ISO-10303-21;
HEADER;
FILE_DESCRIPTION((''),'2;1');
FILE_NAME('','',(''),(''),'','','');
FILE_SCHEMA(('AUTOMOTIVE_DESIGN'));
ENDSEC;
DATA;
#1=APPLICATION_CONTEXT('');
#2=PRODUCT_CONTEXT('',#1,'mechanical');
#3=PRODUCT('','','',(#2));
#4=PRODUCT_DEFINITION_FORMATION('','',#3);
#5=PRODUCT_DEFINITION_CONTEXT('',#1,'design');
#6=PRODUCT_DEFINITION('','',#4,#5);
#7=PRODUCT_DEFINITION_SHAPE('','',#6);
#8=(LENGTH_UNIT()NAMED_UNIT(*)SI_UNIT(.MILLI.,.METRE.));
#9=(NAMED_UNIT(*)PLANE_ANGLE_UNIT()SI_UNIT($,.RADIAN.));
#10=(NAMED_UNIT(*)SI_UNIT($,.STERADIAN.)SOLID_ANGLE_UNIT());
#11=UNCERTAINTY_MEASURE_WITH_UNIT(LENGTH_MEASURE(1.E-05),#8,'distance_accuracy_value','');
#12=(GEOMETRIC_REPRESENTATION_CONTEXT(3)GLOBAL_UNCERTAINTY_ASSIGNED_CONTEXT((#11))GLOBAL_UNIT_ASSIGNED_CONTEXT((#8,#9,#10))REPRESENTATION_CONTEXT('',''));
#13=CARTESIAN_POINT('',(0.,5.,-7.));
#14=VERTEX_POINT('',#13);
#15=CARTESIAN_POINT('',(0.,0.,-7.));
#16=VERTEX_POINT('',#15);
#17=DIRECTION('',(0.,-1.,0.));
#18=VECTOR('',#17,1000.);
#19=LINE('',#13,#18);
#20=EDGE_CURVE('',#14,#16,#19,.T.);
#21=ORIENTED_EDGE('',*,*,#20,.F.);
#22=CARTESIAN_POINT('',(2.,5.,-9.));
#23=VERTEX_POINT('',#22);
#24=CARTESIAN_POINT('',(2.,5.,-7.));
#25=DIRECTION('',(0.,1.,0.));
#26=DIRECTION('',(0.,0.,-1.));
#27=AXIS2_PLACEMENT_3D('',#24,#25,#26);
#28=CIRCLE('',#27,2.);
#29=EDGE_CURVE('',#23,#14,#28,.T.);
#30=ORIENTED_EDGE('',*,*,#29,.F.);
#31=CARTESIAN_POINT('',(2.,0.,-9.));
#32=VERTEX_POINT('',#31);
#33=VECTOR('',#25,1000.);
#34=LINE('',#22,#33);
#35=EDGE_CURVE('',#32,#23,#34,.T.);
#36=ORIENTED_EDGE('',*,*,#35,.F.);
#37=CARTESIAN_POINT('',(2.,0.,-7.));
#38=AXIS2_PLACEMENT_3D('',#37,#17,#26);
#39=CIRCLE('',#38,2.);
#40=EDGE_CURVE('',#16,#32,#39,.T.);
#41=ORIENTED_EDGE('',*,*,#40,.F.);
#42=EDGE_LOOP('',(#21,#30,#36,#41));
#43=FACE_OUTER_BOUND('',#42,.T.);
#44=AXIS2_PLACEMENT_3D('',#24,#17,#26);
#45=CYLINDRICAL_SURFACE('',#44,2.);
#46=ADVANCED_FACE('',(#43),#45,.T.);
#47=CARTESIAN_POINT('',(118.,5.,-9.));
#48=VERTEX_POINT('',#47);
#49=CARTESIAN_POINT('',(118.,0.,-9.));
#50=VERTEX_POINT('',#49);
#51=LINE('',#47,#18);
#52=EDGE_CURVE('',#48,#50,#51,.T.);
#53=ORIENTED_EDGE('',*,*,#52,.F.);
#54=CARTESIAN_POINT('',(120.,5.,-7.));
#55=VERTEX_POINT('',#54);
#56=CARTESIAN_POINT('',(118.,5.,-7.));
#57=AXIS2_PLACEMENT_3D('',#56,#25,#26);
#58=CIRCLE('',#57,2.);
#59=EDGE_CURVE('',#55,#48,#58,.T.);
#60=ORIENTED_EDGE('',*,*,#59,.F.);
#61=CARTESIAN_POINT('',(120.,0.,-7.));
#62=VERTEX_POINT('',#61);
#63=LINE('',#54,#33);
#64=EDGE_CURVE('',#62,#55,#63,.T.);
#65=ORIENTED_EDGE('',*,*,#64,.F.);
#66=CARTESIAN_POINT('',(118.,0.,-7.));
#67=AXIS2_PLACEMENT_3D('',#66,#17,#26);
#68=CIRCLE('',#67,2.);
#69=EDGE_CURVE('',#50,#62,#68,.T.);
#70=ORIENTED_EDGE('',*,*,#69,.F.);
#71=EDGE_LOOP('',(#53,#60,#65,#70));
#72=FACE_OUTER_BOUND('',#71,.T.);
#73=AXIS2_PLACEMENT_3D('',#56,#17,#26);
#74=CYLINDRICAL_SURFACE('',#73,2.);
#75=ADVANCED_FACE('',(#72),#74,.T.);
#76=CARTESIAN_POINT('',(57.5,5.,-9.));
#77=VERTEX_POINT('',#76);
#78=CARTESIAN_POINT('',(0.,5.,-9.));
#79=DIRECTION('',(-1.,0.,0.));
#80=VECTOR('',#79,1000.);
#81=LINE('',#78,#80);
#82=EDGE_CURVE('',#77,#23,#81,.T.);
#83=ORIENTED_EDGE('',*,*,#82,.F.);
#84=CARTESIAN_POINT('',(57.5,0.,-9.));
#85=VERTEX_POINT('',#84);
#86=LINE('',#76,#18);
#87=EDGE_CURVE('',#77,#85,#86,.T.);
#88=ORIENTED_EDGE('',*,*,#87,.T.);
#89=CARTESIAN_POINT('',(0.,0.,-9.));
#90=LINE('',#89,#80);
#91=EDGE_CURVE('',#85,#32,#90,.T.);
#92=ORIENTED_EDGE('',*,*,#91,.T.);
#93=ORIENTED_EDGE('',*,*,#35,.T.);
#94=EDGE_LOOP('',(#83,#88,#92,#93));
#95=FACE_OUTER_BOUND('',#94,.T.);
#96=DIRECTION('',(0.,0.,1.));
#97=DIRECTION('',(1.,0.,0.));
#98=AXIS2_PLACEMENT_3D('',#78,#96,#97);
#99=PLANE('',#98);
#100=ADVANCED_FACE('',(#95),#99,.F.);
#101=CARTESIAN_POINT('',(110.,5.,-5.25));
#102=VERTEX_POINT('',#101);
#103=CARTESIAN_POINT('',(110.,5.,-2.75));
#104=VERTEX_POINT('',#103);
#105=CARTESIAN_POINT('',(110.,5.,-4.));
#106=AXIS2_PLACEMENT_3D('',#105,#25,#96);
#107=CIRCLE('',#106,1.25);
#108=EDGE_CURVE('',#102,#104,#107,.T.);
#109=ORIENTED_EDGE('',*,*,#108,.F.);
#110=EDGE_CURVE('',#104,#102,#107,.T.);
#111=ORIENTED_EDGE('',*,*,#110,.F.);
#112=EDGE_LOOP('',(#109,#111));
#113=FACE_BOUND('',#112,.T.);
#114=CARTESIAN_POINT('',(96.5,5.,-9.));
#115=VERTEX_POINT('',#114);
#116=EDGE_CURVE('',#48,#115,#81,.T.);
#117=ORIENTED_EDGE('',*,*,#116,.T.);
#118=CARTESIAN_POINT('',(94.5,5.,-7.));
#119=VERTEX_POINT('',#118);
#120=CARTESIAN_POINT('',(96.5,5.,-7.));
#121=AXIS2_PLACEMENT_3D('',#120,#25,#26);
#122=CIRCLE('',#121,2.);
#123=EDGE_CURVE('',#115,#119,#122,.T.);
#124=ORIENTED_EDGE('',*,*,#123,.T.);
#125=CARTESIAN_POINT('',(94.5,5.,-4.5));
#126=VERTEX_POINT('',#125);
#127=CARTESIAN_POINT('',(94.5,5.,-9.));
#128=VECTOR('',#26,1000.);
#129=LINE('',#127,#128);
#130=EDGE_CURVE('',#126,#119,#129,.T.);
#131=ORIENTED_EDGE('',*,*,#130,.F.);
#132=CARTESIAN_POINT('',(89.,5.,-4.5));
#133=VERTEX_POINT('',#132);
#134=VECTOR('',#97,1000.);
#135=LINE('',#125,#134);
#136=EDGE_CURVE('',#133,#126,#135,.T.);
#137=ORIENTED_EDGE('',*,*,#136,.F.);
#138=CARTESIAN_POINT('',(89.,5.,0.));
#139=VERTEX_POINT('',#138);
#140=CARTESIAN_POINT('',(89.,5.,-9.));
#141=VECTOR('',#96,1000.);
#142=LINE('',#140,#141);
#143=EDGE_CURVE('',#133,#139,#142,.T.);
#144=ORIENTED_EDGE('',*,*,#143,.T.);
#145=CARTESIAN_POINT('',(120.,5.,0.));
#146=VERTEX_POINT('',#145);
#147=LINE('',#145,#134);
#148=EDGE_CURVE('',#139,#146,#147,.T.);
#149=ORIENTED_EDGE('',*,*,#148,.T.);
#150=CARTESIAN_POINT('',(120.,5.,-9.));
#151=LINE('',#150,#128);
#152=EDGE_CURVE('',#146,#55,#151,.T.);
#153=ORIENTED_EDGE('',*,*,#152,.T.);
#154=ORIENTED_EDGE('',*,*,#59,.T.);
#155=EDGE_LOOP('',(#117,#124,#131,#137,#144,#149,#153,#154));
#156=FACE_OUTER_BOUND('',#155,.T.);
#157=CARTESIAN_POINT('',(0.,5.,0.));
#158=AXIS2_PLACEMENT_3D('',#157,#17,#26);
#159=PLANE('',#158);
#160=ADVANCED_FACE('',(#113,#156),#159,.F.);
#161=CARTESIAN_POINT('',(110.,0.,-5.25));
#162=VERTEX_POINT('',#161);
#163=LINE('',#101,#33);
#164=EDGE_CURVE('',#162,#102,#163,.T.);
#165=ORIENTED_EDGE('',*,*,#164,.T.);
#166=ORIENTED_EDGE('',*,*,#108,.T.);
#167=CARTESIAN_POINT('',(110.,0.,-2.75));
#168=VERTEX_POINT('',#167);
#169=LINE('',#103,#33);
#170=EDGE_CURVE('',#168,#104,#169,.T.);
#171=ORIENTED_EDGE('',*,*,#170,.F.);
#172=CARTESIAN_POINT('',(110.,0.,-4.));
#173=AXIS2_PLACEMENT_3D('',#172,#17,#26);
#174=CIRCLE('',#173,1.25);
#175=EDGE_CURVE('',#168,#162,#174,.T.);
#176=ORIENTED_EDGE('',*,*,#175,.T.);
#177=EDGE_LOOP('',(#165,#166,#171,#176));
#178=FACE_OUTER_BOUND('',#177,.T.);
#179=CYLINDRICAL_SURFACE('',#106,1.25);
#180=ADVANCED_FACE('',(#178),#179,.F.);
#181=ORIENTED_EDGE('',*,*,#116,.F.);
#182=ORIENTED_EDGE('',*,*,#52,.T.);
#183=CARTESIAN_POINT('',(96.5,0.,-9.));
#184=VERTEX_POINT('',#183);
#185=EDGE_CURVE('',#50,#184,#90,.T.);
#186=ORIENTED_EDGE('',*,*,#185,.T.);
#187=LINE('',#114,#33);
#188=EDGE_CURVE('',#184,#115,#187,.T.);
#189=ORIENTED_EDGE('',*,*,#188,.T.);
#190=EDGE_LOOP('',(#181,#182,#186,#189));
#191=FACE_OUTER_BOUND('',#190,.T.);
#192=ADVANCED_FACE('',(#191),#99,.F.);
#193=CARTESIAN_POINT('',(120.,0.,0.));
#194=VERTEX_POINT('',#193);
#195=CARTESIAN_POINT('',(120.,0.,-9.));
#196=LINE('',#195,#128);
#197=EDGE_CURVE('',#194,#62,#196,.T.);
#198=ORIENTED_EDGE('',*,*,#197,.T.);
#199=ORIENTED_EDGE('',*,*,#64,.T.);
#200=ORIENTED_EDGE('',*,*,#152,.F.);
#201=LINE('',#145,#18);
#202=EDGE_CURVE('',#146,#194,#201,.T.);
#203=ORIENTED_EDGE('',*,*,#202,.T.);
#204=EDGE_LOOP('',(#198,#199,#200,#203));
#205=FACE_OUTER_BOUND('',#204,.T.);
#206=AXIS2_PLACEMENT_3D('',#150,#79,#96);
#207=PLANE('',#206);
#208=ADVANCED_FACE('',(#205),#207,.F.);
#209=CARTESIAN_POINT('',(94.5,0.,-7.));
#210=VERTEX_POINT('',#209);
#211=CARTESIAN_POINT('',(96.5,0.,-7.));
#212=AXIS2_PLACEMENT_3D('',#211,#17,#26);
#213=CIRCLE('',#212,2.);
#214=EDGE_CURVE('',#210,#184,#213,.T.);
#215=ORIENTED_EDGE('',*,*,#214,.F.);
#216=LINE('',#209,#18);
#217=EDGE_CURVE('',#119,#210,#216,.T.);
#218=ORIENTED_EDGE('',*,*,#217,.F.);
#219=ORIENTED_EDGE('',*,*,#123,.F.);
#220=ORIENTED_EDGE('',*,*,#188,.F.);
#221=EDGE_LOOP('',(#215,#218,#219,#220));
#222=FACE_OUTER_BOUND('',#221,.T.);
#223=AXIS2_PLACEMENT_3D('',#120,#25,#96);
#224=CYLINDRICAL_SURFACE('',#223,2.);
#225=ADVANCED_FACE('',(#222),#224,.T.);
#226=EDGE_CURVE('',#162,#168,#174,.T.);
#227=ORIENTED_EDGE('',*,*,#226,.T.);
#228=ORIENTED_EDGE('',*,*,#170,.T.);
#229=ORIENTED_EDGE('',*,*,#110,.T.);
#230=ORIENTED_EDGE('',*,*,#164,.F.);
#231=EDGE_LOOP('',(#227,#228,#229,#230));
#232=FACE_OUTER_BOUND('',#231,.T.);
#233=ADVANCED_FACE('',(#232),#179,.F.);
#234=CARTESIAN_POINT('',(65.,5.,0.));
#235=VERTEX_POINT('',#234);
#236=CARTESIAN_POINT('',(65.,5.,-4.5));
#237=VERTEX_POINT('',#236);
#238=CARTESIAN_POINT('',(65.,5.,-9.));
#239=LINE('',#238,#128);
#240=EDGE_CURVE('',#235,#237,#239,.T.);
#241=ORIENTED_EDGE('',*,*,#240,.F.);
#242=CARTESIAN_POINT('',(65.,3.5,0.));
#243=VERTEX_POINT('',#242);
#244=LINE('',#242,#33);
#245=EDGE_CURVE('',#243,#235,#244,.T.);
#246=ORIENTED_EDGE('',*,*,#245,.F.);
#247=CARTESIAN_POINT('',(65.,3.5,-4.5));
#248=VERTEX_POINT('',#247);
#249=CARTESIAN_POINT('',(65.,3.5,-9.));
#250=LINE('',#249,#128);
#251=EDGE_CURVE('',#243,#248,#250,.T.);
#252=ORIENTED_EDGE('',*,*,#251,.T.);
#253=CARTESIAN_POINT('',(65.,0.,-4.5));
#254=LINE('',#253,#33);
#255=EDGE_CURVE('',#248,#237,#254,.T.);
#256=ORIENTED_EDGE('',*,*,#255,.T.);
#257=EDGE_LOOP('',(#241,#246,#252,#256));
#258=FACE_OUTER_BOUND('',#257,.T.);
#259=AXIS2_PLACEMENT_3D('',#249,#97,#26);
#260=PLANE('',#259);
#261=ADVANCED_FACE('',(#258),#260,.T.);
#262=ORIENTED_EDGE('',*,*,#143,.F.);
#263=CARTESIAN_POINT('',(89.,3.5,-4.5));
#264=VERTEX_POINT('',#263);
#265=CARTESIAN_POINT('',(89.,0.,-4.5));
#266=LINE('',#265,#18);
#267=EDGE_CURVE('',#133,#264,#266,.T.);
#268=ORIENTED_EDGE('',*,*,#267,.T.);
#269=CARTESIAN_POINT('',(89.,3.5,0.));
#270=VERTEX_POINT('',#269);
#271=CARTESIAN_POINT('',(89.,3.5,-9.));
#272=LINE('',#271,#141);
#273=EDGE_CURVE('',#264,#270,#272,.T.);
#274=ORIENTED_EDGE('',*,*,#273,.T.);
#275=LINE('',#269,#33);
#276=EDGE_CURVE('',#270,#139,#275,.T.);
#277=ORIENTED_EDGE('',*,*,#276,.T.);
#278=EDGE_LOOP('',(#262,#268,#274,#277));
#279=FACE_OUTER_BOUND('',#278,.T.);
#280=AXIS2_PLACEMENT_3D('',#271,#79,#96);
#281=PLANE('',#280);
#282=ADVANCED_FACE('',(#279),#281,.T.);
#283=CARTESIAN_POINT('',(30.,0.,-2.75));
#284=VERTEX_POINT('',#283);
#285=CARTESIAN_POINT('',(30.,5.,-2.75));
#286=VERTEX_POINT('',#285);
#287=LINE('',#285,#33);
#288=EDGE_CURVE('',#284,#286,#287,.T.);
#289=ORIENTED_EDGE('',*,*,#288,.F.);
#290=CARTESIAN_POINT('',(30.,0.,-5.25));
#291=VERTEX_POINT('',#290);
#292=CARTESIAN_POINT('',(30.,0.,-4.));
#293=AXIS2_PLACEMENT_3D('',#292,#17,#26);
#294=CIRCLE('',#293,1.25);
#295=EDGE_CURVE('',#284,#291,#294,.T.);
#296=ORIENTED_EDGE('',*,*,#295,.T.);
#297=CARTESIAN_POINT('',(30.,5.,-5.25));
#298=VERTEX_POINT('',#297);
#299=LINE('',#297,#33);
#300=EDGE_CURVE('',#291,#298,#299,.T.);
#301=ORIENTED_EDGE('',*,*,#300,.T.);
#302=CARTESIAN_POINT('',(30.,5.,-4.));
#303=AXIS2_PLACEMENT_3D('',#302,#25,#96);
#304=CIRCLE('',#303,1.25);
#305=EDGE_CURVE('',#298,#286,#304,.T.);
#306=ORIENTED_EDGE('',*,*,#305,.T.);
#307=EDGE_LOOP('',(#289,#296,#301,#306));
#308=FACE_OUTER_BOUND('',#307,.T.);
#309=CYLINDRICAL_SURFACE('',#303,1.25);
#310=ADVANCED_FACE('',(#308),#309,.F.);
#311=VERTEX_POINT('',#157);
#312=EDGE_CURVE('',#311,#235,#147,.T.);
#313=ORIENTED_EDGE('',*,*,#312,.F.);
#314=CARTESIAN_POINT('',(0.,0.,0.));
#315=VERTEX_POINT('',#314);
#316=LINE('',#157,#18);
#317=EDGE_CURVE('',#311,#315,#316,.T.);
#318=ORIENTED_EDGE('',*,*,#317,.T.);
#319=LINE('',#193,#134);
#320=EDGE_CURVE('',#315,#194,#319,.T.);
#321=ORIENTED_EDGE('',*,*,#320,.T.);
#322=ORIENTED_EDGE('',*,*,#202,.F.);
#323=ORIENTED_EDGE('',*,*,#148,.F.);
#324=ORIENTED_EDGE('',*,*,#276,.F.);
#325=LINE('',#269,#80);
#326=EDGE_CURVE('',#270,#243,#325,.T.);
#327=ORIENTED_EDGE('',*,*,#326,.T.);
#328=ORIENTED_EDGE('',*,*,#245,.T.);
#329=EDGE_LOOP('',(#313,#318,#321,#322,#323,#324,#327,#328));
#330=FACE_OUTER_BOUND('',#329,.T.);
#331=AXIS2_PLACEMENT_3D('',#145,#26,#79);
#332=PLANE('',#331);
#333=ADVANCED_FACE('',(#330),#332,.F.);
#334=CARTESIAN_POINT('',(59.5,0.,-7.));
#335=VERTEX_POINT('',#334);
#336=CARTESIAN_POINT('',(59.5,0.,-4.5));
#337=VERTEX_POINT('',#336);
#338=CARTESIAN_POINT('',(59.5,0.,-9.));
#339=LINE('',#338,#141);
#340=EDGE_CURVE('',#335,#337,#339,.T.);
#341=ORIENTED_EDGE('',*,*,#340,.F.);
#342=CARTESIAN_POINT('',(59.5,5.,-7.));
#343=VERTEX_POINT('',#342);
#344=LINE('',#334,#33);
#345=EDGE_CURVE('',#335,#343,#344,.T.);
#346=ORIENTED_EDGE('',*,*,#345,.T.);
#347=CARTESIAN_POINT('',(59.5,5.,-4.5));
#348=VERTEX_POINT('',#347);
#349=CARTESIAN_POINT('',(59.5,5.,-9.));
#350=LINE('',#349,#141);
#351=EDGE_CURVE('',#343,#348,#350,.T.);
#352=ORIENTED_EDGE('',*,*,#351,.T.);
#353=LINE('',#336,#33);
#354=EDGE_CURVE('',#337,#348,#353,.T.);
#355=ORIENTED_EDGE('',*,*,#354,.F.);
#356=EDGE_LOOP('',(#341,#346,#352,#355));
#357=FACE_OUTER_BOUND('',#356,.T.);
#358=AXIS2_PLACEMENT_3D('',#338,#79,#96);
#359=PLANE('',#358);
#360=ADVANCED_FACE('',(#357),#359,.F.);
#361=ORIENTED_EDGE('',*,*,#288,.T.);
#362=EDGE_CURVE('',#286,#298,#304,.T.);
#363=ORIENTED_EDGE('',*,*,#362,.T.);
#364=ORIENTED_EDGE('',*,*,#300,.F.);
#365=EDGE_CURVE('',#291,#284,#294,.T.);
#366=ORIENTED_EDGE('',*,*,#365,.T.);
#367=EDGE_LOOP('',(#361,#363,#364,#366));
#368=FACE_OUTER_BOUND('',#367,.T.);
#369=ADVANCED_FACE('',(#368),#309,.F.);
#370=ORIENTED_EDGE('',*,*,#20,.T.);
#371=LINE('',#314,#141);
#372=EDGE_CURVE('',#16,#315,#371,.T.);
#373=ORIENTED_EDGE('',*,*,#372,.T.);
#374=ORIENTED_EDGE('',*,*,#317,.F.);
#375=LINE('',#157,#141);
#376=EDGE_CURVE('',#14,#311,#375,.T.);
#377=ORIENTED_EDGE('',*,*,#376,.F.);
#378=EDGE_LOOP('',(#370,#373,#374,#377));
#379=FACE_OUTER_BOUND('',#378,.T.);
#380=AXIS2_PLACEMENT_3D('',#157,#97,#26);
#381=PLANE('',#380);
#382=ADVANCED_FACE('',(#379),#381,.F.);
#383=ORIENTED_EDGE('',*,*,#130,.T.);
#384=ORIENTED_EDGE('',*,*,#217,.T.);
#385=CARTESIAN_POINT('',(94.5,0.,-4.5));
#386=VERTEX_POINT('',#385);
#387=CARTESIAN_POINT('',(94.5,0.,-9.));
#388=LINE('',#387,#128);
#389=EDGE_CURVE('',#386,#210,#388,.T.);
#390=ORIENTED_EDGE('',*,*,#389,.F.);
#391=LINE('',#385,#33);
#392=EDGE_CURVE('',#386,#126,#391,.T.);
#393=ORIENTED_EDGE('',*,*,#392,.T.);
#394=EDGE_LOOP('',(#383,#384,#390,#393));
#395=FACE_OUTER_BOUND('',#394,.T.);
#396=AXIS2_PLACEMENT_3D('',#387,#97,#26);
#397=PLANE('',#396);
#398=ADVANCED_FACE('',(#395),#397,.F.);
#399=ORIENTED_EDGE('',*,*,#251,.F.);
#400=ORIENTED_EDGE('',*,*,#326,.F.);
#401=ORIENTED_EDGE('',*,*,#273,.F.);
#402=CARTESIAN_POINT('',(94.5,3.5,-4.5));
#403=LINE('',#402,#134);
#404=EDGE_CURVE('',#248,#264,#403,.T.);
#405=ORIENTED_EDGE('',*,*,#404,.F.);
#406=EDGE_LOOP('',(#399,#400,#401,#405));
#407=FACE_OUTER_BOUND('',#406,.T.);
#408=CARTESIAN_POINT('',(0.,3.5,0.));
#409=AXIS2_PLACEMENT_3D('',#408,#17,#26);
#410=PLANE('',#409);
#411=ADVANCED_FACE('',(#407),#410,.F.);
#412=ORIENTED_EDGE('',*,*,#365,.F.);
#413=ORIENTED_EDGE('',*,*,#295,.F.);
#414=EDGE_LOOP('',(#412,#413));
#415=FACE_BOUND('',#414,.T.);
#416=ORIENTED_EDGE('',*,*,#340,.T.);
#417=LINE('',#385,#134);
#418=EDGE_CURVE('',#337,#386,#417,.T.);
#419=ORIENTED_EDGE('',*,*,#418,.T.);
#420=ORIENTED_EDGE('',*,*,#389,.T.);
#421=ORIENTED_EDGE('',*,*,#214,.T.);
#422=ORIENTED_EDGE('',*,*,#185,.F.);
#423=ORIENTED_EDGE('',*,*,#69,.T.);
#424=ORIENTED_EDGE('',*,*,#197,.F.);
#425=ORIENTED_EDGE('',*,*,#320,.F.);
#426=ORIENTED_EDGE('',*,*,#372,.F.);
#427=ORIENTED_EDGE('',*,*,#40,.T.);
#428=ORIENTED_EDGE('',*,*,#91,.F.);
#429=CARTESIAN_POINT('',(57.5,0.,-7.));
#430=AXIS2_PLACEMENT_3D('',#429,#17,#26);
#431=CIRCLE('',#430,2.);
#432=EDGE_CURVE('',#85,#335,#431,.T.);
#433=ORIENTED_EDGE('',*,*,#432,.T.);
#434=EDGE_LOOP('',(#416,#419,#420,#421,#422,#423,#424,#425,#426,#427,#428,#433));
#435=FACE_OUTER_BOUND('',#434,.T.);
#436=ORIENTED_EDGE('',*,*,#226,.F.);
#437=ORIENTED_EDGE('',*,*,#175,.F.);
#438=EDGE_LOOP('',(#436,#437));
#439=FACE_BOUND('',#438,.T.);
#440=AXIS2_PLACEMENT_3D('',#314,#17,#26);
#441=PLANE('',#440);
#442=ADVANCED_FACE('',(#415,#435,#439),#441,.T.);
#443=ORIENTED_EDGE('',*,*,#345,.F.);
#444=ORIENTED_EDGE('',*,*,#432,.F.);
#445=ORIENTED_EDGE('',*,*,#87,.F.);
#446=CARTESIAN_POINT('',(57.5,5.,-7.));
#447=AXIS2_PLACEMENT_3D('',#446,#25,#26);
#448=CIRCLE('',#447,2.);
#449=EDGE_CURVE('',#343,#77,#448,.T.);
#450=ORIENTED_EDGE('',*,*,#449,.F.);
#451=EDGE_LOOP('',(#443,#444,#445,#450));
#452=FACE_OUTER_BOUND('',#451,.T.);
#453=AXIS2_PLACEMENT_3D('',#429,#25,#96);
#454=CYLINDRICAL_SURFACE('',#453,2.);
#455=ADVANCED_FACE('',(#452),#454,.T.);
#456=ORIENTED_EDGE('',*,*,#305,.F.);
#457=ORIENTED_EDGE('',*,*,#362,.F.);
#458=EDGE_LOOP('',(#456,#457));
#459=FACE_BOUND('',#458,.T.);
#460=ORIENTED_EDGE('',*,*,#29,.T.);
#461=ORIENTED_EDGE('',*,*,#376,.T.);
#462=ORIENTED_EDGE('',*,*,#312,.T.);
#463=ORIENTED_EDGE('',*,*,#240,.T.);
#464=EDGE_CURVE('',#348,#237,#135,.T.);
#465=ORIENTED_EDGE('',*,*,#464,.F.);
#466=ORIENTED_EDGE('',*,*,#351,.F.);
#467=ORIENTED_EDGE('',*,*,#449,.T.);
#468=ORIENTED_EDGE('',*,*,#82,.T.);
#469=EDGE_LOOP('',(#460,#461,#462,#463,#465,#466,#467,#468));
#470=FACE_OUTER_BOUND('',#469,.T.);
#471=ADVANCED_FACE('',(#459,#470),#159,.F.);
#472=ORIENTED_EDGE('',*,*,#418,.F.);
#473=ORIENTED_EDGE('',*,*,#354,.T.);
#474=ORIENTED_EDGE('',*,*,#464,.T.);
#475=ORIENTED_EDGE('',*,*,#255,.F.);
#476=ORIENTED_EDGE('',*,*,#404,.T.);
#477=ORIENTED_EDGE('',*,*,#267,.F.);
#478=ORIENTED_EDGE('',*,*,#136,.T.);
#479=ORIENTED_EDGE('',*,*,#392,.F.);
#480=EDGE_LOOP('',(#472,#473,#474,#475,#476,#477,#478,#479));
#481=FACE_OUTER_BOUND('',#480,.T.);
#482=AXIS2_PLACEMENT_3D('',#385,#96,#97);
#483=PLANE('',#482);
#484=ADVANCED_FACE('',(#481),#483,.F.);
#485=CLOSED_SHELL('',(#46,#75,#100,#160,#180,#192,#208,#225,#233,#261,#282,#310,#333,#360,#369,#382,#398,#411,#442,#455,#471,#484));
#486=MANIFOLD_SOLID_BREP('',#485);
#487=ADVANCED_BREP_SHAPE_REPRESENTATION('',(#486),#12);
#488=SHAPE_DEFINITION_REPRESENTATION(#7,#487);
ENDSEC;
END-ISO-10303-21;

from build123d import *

# Parameters (mm, degrees)
SKETCH1_W             = 120
SKETCH1_H             = 9
BOSS_EXTRUDE1_DEPTH   = 5
M3_TAPPED_HOLE1_D     = 2.5
M3_TAPPED_HOLE1_DEPTH = 8.5
FILLET1_R             = 2
SKETCH4_W             = 35
SKETCH4_H             = 4.5
CUT_EXTRUDE1_DEPTH    = 121.440856855
FILLET2_R             = 2
SKETCH5_W             = 24
SKETCH5_H             = 9
CUT_EXTRUDE2_DEPTH    = 1.5


with BuildPart() as part:
    # Sketch1 → Boss-Extrude1 (new body)
    with BuildSketch(Plane(origin=(0, 0, 0), x_dir=(1, 0, 0), z_dir=(0, 1, 0))):
        with Locations((60, 4.5)):
            Rectangle(SKETCH1_W, SKETCH1_H)
    extrude(amount=BOSS_EXTRUDE1_DEPTH)

    # M3 Tapped Hole1
    with Locations(Plane(origin=(0, 5, 0), x_dir=(-1, 0, 0), z_dir=(0, 1, 0))):
        with Locations((-30, -4), (-110, -4)):
            Hole(M3_TAPPED_HOLE1_D / 2, depth=M3_TAPPED_HOLE1_DEPTH)

    # Fillet1
    fillet1_edges = [part.edges().sort_by_distance(p)[0] for p in [
        (0, 2.5, -9),
        (120, 2.5, -9),
    ]]
    fillet(fillet1_edges, radius=FILLET1_R)

    # Sketch4 → Cut-Extrude1 (cut, through all)
    with BuildSketch(Plane(origin=(0, 5, 0), x_dir=(-1, 0, 0), z_dir=(0, 1, 0))):
        with Locations((-77, -6.75)):
            Rectangle(SKETCH4_W, SKETCH4_H)
    extrude(amount=-CUT_EXTRUDE1_DEPTH, mode=Mode.SUBTRACT)

    # Fillet2
    fillet2_edges = [part.edges().sort_by_distance(p)[0] for p in [
        (94.5, 2.5, -9),
        (59.5, 2.5, -9),
    ]]
    fillet(fillet2_edges, radius=FILLET2_R)

    # Sketch5 → Cut-Extrude2 (cut)
    with BuildSketch(Plane.XZ.offset(-5)):
        with Locations((77, -4.5)):
            Rectangle(SKETCH5_W, SKETCH5_H)
    extrude(amount=CUT_EXTRUDE2_DEPTH, mode=Mode.SUBTRACT)


solid = part.part
